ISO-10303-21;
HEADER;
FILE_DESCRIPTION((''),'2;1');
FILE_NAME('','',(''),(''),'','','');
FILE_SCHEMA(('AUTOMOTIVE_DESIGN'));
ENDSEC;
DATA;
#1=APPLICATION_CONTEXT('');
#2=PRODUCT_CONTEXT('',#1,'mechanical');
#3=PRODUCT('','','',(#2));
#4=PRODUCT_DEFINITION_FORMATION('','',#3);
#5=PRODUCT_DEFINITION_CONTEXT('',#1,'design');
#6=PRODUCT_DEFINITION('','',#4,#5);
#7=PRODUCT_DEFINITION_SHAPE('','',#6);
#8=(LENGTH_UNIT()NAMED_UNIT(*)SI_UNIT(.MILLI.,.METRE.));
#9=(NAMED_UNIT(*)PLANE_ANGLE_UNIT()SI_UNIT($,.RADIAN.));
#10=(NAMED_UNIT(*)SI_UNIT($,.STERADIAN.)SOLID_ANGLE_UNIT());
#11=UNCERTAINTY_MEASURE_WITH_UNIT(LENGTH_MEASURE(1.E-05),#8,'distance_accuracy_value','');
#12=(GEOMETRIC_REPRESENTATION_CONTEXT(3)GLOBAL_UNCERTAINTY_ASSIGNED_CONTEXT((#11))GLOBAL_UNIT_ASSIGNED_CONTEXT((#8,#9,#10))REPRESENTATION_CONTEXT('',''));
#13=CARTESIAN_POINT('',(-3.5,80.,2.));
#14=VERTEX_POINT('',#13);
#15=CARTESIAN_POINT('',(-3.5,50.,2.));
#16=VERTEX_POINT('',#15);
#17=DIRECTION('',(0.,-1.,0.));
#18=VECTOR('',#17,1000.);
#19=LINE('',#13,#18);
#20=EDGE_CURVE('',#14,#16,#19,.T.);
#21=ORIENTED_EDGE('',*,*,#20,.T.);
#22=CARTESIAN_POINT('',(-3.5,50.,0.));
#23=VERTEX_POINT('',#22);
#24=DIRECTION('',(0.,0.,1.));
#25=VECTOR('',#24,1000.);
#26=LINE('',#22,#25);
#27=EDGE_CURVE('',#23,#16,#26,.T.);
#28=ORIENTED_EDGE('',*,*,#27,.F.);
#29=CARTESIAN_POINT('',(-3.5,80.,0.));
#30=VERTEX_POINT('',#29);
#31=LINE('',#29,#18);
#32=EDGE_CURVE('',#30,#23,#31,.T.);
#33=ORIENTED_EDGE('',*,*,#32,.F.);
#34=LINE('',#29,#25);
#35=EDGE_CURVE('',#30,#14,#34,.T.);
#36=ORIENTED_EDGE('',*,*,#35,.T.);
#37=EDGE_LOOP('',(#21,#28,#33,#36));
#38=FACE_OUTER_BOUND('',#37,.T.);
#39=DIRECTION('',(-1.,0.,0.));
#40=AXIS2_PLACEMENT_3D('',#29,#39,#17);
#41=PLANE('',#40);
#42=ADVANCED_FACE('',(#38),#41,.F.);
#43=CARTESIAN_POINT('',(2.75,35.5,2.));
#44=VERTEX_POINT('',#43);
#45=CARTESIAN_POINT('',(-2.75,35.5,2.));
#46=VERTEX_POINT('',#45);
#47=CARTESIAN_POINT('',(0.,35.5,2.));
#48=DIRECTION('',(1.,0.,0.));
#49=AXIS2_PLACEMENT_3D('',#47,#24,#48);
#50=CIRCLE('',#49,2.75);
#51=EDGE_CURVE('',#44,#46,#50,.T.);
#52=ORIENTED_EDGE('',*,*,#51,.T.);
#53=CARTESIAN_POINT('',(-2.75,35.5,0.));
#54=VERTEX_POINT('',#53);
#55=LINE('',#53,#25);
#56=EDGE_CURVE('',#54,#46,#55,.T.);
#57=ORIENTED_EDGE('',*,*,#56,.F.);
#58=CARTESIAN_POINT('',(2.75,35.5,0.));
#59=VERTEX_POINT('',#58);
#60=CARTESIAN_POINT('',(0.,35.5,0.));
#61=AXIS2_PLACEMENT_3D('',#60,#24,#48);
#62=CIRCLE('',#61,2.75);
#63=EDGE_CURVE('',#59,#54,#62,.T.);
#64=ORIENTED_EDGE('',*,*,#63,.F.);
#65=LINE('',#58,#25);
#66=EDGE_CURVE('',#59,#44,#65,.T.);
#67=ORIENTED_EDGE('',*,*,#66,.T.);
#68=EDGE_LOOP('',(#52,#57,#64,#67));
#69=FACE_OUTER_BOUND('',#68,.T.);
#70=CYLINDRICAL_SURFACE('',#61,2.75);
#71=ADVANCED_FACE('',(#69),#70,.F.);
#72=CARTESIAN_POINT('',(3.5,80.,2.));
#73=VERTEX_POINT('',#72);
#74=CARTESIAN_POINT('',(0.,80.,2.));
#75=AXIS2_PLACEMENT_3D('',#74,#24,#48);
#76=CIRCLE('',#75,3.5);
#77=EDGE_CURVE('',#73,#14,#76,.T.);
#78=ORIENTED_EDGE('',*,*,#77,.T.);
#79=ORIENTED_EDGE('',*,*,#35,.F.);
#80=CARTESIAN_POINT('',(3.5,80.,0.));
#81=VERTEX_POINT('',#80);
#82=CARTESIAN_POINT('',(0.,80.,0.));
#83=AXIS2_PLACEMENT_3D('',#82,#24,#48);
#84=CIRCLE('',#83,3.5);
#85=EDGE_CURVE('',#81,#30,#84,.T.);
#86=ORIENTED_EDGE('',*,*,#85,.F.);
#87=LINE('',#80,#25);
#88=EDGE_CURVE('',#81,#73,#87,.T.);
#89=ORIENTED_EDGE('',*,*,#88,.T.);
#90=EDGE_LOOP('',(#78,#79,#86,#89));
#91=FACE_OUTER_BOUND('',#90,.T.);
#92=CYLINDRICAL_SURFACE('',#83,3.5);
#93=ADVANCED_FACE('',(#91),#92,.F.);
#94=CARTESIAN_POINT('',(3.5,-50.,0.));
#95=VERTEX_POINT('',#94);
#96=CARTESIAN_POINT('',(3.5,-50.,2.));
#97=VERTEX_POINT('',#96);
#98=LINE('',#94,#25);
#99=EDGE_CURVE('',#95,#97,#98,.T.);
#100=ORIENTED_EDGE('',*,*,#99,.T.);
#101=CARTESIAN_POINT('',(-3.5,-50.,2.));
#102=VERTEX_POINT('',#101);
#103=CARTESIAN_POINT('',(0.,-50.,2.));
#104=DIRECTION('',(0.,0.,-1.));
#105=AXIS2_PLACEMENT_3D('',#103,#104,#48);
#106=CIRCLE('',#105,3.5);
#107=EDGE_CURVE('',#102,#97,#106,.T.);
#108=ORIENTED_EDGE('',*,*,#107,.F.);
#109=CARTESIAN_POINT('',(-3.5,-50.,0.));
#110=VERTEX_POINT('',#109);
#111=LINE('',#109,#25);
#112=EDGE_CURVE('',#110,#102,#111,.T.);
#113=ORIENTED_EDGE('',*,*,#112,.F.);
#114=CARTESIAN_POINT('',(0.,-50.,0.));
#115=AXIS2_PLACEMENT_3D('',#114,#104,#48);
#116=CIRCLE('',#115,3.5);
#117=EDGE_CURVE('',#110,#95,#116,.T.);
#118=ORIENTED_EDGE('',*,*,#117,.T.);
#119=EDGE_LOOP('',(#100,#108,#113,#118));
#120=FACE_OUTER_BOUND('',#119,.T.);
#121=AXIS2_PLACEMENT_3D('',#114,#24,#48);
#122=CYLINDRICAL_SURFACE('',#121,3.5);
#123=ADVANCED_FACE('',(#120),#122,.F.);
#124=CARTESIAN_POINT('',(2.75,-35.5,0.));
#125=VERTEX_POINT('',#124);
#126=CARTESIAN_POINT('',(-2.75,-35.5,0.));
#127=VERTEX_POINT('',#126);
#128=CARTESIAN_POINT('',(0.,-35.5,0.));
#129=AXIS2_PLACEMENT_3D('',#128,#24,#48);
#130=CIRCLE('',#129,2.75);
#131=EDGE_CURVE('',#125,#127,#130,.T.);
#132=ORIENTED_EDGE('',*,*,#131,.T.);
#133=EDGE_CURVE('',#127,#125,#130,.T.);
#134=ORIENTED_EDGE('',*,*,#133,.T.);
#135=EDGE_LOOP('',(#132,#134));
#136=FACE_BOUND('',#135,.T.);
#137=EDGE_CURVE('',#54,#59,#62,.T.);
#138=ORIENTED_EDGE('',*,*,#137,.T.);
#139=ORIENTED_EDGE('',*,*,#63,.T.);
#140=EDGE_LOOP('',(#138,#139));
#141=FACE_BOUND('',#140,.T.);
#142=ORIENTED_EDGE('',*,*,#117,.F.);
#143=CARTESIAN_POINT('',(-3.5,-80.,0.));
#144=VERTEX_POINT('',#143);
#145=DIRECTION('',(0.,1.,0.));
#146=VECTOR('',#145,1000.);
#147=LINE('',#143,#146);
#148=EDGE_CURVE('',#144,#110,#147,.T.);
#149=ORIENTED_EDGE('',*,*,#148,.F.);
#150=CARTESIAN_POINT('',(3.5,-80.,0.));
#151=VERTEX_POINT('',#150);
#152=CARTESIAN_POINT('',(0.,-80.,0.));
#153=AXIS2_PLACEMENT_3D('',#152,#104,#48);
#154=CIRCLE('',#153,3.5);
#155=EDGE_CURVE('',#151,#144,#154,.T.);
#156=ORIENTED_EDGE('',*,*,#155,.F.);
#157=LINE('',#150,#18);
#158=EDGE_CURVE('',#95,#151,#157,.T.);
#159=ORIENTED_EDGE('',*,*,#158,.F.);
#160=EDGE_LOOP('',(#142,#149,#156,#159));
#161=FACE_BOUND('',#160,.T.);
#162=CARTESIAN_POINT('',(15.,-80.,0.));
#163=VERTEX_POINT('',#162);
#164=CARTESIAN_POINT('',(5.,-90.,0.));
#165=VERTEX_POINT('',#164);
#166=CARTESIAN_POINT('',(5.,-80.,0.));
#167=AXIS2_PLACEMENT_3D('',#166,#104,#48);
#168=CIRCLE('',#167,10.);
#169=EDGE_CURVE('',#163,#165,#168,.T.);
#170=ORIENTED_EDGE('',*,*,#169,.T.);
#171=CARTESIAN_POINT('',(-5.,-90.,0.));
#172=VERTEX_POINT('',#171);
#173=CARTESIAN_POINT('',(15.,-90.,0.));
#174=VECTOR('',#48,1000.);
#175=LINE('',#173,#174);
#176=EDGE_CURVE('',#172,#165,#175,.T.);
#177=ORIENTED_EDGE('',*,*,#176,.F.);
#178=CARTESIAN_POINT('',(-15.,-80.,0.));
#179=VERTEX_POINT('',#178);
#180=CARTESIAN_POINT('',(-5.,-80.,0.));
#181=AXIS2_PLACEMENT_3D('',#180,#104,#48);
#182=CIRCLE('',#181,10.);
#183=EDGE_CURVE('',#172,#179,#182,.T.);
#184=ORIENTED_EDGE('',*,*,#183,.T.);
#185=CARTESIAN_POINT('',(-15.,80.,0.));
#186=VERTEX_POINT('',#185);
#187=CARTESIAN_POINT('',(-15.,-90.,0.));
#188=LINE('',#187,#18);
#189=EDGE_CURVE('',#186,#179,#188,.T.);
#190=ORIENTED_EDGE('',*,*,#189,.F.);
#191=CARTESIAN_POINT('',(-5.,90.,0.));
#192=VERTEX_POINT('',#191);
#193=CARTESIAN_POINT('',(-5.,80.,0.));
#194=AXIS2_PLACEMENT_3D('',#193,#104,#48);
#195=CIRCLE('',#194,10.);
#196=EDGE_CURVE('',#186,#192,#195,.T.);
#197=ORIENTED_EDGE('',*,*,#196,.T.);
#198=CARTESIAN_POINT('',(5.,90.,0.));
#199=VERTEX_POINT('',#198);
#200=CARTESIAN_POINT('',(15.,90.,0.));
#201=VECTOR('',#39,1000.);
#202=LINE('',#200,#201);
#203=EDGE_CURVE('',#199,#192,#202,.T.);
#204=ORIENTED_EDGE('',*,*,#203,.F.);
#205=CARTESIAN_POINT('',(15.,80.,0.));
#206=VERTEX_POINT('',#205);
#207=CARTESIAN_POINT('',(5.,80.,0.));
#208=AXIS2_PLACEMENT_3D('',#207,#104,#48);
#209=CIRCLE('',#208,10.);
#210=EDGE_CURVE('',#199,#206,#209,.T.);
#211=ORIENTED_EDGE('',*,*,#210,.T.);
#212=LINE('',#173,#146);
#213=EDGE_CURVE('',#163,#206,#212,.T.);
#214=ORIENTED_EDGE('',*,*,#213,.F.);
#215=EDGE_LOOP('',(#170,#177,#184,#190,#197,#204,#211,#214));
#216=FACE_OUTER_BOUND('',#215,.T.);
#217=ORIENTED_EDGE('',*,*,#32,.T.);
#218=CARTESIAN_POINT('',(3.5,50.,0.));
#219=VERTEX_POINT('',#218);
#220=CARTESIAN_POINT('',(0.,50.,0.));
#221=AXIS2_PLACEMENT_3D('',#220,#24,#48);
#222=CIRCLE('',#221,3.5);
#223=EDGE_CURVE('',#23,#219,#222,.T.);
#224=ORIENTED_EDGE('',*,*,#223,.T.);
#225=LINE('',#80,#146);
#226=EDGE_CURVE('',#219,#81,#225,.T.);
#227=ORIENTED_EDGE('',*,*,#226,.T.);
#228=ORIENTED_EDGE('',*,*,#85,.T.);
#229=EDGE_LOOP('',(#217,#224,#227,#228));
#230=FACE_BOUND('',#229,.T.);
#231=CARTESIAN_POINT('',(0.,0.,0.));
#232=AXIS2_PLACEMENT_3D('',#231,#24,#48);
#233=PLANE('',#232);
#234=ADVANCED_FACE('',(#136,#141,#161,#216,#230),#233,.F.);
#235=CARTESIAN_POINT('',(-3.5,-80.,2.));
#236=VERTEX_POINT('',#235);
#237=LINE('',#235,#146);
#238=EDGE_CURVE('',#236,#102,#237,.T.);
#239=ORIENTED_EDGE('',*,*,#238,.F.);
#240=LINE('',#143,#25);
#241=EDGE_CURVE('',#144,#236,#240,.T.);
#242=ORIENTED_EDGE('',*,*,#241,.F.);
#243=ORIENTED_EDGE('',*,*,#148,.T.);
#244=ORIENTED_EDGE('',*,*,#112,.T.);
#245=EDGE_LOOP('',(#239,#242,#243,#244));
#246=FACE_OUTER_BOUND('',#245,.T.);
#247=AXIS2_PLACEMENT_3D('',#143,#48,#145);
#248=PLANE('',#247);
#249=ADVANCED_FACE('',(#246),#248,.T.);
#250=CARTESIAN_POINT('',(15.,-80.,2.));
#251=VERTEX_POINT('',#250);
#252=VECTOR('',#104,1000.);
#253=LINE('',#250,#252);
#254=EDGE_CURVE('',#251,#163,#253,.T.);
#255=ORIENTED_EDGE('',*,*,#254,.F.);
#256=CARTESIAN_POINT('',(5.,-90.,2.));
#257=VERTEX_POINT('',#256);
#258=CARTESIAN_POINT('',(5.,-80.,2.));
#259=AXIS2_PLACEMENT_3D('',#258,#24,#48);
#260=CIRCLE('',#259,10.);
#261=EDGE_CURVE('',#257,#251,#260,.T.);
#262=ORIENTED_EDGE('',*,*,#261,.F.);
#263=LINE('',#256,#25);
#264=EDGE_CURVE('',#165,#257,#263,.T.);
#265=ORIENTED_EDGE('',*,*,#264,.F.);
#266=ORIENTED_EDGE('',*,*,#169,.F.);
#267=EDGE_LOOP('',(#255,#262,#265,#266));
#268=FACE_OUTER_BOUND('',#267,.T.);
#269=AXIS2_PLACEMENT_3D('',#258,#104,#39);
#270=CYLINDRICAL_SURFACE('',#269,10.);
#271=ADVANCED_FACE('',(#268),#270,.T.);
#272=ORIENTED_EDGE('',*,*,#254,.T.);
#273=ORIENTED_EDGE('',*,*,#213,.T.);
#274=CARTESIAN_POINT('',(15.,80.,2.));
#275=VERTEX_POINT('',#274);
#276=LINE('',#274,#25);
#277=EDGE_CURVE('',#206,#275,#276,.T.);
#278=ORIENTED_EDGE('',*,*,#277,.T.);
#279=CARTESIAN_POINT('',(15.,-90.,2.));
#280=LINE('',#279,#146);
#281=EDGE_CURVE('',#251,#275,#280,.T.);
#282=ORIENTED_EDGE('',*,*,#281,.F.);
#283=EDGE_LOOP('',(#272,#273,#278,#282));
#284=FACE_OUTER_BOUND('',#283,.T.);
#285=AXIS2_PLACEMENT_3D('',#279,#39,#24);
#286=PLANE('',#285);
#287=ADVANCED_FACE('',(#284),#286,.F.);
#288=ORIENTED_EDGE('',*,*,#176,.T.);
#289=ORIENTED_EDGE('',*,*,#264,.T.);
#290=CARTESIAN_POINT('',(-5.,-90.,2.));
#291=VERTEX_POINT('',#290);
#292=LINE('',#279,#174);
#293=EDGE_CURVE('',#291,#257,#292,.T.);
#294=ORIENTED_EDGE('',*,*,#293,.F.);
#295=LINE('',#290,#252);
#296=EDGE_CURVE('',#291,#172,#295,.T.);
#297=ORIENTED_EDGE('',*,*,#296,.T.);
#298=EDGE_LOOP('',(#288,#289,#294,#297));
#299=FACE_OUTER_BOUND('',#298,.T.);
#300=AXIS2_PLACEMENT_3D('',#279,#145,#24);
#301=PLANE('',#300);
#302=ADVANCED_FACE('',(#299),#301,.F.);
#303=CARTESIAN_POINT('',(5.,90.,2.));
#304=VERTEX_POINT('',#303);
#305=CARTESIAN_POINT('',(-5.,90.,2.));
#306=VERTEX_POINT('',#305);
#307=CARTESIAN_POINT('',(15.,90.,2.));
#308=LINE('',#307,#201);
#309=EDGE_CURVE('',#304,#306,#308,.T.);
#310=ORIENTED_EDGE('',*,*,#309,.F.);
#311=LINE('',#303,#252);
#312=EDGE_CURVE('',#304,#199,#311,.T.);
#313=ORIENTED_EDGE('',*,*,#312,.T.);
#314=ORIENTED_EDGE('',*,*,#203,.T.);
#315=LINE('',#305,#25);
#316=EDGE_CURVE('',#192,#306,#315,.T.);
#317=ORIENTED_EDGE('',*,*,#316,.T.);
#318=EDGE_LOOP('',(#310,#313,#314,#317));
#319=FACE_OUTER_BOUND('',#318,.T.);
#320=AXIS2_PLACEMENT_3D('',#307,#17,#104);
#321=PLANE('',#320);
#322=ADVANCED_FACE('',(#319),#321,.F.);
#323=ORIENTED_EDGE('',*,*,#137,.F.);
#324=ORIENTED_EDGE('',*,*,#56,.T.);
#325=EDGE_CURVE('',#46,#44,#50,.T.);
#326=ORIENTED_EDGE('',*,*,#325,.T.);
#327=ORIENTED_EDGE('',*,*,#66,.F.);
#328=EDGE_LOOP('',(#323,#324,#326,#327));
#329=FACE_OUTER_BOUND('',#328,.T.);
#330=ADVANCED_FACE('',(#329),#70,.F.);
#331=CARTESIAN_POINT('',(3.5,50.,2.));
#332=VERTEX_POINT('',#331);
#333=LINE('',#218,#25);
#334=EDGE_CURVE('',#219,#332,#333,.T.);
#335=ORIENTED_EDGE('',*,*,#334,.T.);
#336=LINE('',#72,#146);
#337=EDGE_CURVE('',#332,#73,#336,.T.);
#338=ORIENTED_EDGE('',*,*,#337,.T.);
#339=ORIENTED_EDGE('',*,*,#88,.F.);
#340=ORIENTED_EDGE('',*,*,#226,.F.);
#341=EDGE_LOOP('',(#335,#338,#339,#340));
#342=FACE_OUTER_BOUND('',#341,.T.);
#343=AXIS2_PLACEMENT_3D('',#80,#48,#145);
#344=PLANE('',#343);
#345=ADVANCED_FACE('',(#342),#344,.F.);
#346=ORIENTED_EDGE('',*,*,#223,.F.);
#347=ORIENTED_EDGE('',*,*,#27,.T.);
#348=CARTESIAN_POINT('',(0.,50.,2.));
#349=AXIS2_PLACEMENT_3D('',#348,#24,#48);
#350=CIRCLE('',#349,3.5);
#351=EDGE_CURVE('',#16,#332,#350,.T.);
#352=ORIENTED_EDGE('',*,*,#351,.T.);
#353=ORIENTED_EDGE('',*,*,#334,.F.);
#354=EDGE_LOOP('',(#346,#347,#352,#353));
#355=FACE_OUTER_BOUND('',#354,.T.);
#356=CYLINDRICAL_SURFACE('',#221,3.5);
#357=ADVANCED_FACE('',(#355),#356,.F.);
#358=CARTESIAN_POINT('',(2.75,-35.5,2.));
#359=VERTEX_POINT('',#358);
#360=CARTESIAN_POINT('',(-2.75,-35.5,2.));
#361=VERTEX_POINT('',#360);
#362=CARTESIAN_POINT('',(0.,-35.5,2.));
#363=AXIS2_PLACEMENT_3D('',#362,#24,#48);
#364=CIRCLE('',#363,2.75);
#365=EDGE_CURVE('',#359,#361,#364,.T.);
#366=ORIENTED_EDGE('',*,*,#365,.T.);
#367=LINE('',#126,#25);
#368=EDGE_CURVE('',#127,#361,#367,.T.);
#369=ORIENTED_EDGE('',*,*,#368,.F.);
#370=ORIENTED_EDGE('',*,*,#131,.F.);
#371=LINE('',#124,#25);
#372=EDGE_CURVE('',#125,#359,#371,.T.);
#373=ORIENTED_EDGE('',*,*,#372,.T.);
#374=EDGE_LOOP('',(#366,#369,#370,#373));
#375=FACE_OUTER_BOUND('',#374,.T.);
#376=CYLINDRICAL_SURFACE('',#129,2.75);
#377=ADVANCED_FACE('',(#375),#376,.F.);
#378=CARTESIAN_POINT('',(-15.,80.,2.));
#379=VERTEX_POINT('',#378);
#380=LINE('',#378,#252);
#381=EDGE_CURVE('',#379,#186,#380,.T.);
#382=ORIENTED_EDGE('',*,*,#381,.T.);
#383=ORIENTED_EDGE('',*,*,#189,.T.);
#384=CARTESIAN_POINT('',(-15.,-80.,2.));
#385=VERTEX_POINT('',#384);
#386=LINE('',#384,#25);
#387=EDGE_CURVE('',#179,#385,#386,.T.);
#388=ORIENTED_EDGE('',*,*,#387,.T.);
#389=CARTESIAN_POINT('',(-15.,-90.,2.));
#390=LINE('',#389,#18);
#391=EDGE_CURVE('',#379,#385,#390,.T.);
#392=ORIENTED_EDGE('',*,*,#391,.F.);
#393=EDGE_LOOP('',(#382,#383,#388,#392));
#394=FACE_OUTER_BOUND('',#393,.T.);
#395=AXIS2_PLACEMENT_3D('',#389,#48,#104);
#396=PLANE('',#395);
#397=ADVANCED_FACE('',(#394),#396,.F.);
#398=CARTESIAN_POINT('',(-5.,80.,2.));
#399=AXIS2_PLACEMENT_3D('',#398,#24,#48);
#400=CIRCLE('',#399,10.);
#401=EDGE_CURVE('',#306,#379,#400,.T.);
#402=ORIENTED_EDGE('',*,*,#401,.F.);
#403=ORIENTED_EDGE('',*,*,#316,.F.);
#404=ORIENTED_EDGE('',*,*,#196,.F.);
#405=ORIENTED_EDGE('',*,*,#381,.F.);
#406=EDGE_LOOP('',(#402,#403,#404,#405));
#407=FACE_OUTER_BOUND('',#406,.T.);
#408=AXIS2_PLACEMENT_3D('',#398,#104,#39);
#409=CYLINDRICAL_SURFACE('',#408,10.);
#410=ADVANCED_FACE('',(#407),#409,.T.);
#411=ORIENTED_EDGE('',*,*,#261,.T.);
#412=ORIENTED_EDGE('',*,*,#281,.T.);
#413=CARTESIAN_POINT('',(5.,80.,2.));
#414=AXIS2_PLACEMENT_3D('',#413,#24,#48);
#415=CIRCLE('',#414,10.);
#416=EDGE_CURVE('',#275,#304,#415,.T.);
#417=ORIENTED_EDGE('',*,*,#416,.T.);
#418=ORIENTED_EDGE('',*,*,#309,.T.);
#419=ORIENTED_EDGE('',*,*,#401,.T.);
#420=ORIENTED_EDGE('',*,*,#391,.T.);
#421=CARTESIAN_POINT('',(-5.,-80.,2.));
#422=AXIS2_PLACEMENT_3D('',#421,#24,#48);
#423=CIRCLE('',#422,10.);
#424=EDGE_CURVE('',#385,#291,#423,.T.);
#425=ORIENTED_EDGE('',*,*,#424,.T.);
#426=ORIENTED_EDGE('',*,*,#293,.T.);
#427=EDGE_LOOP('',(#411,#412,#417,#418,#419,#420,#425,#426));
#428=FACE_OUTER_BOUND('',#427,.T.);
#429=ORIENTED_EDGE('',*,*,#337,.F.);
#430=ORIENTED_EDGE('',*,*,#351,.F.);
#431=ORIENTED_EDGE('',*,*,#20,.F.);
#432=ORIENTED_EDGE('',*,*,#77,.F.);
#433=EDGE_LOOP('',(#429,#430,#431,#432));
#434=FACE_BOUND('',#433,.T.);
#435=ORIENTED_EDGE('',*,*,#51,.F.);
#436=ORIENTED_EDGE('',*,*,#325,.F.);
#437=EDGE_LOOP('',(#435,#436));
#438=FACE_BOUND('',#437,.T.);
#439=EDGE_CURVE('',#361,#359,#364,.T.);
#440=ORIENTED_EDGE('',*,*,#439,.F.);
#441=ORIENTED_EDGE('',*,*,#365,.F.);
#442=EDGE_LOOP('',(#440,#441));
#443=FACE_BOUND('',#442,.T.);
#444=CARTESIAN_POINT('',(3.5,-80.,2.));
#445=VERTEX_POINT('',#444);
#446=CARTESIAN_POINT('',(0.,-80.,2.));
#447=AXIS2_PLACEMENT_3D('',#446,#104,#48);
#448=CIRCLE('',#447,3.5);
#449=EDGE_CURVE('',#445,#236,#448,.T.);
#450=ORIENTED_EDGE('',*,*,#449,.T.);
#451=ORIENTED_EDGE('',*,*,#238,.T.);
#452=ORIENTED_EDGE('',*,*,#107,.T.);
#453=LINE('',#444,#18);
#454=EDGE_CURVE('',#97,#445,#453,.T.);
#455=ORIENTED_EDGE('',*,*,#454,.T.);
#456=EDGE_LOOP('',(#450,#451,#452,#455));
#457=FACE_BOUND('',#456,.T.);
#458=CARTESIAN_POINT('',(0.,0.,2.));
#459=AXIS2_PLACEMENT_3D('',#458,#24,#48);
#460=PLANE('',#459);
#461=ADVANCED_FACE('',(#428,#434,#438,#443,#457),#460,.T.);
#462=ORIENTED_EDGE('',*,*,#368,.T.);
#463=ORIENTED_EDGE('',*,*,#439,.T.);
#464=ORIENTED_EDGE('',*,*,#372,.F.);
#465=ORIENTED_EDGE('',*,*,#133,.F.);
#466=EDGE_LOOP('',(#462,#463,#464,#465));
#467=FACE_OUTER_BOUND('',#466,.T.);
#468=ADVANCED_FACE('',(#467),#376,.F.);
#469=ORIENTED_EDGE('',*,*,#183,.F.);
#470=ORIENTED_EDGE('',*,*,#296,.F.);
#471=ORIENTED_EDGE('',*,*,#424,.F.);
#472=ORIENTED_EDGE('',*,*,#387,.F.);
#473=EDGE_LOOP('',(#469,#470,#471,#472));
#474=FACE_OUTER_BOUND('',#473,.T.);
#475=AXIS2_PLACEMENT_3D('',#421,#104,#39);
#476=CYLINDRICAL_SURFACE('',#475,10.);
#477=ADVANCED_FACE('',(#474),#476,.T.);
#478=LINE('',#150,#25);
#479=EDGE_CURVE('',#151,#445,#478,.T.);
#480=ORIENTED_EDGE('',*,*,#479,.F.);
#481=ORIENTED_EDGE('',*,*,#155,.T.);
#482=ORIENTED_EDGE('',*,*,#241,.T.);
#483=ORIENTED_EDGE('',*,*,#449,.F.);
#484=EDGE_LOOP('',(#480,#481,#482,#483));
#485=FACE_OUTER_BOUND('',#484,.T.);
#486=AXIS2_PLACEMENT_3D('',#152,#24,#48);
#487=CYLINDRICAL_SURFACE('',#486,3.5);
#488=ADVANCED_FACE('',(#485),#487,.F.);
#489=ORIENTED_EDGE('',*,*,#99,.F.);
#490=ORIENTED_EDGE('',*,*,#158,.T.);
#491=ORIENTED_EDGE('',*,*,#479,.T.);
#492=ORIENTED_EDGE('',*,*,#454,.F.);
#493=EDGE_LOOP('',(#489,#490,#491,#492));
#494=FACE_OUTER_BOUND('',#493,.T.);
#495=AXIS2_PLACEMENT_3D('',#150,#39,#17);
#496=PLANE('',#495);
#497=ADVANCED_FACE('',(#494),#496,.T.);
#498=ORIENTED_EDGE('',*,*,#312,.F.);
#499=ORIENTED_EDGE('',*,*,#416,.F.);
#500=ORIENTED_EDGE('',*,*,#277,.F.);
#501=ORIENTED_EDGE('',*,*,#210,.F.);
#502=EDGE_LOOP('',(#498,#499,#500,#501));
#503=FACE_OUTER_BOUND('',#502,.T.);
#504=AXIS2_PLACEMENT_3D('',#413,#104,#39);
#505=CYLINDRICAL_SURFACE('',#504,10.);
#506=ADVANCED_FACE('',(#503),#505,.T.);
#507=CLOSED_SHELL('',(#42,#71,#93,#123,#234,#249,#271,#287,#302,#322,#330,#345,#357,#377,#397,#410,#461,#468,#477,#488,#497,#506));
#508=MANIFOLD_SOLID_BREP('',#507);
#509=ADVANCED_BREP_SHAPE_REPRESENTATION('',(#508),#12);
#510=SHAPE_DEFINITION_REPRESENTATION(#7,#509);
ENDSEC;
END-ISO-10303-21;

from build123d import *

# Parameters (mm, degrees)
SKETCH1_W           = 30
SKETCH1_H           = 180
BOSS_EXTRUDE1_DEPTH = 2
FILLET1_R           = 10
CUT_EXTRUDE1_DEPTH  = 92.263355187
SKETCH3_R           = 2.75
CUT_EXTRUDE2_DEPTH  = 92.263355187


with BuildPart() as part:
    # Sketch1 → Boss-Extrude1 (new body)
    with BuildSketch(Plane.XY):
        Rectangle(SKETCH1_W, SKETCH1_H)
    extrude(amount=BOSS_EXTRUDE1_DEPTH)

    # Fillet1
    fillet1_edges = [part.edges().sort_by_distance(p)[0] for p in [
        (-15, 90, 1),
        (15, 90, 1),
        (15, -90, 1),
        (-15, -90, 1),
    ]]
    fillet(fillet1_edges, radius=FILLET1_R)

    # Sketch2 → Cut-Extrude1 (cut, through all)
    with BuildSketch(Plane.XY.offset(2)):
        with BuildLine():
            Line((3.5, 80), (3.5, 50))
            ThreePointArc((3.5, 50), (0, 46.5), (-3.5, 50))
            Line((-3.5, 50), (-3.5, 80))
            ThreePointArc((-3.5, 80), (0, 83.5), (3.5, 80))
        make_face()
    cut_extrude1 = extrude(amount=-CUT_EXTRUDE1_DEPTH, mode=Mode.SUBTRACT)

    # Mirror1: Cut-Extrude1 across plane
    add(cut_extrude1.mirror(Plane.ZX), mode=Mode.SUBTRACT)

    # Sketch3 → Cut-Extrude2 (cut, through all)
    with BuildSketch(Plane.XY.offset(2)):
        with Locations((0, -35.5)):
            Circle(SKETCH3_R)
        with Locations((0, 35.5)):
            Circle(SKETCH3_R)
    extrude(amount=-CUT_EXTRUDE2_DEPTH, mode=Mode.SUBTRACT)


solid = part.part
